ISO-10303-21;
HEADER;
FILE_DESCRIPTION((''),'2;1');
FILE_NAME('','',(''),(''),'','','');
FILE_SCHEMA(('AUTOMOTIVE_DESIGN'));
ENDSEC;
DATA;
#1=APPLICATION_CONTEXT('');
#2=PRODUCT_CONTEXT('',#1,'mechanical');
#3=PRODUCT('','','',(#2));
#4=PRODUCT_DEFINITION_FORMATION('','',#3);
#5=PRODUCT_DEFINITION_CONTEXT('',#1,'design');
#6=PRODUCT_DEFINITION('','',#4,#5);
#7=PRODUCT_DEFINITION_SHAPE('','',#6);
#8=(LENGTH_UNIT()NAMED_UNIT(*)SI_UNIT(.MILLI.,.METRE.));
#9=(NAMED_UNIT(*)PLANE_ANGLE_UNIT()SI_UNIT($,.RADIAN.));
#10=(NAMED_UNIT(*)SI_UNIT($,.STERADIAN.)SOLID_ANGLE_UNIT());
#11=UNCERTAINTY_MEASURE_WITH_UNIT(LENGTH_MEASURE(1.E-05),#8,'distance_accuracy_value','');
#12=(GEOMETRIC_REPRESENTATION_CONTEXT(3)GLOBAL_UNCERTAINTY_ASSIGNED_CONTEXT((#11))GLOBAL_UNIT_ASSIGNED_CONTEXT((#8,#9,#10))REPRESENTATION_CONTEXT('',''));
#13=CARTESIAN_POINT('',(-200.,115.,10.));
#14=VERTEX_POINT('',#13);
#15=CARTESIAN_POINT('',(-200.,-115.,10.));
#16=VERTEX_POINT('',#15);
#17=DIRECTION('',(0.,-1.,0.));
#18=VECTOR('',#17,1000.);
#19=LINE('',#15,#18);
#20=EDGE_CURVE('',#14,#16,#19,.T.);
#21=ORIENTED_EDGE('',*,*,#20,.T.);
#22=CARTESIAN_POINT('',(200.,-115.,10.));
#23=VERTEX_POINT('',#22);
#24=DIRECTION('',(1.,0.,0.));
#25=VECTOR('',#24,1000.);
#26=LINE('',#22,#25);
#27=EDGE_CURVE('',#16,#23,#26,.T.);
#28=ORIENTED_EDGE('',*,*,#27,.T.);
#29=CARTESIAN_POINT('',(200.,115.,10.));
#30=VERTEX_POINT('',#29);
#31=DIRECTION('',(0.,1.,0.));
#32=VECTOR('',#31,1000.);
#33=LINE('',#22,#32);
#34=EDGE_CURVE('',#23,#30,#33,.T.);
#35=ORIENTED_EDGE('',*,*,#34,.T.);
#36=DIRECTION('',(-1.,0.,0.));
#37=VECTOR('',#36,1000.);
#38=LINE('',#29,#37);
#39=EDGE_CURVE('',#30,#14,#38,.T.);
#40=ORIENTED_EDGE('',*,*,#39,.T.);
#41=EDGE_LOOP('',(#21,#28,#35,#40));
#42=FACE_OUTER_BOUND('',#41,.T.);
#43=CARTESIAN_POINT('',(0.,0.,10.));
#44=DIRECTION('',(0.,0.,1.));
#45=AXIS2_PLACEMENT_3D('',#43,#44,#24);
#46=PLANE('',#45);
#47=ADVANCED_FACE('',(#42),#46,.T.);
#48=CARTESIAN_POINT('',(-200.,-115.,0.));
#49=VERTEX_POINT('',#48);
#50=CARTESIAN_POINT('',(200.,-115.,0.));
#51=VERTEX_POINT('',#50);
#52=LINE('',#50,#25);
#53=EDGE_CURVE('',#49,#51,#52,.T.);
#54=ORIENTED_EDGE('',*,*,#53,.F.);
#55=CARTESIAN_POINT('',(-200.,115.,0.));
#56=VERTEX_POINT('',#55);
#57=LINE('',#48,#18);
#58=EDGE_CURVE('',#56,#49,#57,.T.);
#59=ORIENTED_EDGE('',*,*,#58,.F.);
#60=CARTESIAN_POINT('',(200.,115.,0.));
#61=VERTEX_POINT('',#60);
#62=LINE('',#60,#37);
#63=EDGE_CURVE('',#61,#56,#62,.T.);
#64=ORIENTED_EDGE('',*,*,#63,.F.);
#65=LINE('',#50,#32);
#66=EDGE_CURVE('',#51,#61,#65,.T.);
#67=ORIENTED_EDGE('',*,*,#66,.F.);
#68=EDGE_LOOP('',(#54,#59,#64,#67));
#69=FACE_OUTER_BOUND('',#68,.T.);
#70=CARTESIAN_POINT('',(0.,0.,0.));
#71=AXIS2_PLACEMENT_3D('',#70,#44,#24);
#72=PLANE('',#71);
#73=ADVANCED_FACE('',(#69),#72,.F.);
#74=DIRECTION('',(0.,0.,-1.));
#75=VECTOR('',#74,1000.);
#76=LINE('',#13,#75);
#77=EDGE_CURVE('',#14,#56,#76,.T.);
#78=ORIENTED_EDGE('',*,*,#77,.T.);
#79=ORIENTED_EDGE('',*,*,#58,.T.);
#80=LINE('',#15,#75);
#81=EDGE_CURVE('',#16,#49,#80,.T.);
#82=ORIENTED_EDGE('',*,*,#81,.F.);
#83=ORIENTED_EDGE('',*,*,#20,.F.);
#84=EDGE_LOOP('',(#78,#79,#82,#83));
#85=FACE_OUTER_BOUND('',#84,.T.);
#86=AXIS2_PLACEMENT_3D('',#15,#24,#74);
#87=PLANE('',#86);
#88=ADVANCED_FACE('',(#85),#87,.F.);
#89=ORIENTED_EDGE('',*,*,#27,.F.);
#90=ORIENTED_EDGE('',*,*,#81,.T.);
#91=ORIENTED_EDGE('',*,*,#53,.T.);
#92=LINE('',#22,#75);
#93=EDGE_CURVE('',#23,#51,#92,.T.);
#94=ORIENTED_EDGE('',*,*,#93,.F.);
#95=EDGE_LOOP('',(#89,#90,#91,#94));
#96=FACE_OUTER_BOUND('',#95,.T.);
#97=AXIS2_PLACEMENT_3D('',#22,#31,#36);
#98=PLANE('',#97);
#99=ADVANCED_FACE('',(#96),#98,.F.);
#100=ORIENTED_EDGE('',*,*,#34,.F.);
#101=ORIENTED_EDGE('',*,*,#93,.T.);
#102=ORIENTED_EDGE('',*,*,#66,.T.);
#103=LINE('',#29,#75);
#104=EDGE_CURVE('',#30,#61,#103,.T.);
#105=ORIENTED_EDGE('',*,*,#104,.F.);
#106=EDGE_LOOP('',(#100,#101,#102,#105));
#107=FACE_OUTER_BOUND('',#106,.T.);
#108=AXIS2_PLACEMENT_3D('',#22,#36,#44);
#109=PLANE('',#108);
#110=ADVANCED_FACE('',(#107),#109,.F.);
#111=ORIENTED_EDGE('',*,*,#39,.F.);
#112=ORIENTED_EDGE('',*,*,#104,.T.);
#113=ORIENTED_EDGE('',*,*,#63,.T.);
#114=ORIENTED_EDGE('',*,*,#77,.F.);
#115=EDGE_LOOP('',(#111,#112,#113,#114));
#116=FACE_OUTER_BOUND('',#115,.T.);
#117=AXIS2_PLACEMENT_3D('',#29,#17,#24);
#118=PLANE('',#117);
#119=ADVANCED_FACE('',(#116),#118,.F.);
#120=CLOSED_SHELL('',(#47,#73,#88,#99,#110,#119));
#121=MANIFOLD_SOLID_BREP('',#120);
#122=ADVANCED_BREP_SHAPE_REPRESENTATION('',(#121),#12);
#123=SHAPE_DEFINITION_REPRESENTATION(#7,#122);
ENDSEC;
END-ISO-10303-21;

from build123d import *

# Parameters (mm, degrees)
SKETCH1_W           = 400
SKETCH1_H           = 230
BOSS_EXTRUDE1_DEPTH = 10


with BuildPart() as part:
    # Sketch1 → Boss-Extrude1 (new body)
    with BuildSketch(Plane.XY):
        Rectangle(SKETCH1_W, SKETCH1_H)
    extrude(amount=BOSS_EXTRUDE1_DEPTH)


solid = part.part
